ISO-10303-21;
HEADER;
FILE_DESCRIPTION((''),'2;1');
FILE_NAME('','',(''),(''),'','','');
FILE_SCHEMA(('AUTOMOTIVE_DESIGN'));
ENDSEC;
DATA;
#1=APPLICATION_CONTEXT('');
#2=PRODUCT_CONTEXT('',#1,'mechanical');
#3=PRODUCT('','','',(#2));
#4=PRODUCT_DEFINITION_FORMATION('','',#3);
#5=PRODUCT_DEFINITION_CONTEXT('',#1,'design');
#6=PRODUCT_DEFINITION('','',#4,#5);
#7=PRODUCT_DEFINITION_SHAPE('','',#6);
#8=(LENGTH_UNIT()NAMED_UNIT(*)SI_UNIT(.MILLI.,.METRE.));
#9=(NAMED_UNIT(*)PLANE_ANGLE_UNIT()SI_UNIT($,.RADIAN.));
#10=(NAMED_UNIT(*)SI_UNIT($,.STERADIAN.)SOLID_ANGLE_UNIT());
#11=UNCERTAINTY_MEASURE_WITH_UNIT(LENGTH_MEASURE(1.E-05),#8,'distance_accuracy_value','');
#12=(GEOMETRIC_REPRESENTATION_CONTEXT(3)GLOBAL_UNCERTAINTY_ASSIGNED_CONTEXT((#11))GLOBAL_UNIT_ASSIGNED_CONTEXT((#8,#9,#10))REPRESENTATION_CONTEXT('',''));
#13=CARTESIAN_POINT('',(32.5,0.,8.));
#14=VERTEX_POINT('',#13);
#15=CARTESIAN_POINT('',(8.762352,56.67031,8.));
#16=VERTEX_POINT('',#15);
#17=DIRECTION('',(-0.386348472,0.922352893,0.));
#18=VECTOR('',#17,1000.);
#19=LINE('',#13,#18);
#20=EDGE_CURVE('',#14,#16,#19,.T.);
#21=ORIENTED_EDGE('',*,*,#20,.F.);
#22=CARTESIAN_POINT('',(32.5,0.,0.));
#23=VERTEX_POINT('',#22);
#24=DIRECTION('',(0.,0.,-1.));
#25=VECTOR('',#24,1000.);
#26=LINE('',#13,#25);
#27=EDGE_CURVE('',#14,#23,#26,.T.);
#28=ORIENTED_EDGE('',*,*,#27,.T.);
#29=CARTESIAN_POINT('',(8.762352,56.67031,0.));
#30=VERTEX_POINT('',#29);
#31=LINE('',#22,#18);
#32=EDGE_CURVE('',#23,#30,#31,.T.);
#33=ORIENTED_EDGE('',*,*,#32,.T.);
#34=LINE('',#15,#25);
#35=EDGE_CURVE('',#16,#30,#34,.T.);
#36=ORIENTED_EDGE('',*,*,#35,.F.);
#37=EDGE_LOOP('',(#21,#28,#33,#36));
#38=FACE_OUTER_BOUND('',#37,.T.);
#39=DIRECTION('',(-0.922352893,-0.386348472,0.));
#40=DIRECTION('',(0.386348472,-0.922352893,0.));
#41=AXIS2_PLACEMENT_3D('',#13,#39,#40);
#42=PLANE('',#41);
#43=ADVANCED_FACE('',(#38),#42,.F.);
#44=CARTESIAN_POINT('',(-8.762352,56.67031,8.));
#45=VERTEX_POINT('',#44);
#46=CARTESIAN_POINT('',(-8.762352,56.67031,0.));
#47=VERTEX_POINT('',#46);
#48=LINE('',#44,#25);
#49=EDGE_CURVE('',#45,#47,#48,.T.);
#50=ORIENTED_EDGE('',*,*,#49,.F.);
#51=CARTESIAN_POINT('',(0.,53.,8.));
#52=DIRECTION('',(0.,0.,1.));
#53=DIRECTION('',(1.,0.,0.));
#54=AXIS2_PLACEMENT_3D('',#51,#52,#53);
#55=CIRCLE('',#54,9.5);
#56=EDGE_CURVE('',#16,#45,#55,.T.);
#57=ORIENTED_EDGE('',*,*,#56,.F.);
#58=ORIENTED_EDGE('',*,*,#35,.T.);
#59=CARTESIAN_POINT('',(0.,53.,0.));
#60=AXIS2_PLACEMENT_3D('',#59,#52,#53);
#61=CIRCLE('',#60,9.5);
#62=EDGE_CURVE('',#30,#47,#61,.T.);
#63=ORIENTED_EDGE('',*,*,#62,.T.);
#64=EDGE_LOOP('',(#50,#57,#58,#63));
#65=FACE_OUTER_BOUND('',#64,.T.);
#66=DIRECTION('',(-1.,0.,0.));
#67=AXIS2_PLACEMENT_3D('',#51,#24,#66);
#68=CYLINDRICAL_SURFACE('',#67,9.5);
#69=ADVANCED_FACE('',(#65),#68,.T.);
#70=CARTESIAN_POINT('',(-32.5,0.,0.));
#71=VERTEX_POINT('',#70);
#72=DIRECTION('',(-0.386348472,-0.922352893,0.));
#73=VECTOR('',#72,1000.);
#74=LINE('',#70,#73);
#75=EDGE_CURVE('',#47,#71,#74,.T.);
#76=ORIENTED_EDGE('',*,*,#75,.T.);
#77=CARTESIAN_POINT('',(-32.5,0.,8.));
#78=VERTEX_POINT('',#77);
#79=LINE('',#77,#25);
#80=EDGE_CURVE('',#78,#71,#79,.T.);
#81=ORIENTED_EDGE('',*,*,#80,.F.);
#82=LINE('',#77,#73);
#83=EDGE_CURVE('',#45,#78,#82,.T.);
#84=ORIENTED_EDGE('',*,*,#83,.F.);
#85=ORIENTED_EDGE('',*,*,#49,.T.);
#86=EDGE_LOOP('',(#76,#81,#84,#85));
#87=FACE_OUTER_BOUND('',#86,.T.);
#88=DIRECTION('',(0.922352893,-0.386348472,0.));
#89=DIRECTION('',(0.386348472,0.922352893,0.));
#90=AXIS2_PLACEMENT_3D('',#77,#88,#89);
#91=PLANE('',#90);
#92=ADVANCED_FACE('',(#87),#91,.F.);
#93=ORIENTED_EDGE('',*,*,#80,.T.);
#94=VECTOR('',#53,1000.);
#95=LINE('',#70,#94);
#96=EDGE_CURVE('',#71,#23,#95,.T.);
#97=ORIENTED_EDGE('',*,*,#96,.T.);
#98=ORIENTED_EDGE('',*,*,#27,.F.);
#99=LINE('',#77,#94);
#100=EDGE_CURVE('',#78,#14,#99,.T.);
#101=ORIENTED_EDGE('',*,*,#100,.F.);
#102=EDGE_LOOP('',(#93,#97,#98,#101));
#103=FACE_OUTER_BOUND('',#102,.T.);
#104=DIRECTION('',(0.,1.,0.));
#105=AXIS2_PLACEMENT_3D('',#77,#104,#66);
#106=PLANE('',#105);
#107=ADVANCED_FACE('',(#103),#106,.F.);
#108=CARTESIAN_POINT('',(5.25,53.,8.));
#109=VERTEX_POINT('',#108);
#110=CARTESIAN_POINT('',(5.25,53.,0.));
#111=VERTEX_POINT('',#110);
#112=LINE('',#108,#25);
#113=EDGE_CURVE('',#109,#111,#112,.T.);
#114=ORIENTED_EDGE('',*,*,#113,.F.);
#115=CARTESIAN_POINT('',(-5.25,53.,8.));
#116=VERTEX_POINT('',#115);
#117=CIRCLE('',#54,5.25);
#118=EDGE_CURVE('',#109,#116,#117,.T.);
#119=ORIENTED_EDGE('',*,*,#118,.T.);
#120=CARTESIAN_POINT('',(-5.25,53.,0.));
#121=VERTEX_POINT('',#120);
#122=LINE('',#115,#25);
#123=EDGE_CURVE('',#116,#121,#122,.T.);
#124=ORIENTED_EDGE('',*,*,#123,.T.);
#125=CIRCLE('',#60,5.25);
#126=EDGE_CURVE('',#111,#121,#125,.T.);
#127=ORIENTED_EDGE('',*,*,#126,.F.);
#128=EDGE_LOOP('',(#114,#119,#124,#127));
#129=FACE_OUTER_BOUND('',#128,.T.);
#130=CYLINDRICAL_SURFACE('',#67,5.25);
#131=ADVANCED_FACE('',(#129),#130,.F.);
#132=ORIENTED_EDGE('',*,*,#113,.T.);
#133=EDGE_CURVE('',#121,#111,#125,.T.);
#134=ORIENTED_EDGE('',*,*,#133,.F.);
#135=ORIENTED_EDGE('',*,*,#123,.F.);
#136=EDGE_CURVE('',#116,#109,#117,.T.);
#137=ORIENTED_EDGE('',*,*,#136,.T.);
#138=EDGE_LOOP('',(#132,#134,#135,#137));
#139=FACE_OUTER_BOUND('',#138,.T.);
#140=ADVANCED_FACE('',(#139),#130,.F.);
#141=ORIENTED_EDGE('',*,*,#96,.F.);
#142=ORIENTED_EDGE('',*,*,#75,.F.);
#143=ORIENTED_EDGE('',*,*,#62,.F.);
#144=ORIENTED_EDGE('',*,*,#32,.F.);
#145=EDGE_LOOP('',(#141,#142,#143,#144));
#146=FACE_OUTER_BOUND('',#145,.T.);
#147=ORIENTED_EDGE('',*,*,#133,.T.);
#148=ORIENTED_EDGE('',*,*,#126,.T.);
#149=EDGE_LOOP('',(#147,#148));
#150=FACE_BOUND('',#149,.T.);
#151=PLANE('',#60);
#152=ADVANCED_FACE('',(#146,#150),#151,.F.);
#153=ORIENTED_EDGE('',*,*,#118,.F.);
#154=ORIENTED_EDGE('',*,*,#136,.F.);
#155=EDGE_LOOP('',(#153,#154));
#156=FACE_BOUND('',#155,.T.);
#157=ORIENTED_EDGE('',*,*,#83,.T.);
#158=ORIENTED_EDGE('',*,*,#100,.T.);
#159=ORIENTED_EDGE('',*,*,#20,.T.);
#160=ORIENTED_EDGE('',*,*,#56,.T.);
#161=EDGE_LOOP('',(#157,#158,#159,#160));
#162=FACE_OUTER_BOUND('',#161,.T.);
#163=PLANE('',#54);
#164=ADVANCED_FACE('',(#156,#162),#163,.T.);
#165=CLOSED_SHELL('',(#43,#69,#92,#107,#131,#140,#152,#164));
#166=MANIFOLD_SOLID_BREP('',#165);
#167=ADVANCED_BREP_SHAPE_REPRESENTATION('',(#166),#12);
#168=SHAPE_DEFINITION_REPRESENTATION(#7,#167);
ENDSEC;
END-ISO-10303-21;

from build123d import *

# Parameters (mm, degrees)
SKETCH1_R           = 5.25
BOSS_EXTRUDE1_DEPTH = 8


with BuildPart() as part:
    # Sketch1 → Boss-Extrude1 (new body)
    with BuildSketch(Plane.XY):
        with BuildLine():
            Line((-32.5, 0), (32.5, 0))
            Line((32.5, 0), (8.762352479, 56.670310482))
            ThreePointArc((8.762352479, 56.670310482), (0, 62.5), (-8.762352479, 56.670310482))
            Line((-8.762352479, 56.670310482), (-32.5, 0))
        make_face()
        with Locations((0, 53)):
            Circle(SKETCH1_R, mode=Mode.SUBTRACT)
    extrude(amount=BOSS_EXTRUDE1_DEPTH)


solid = part.part
